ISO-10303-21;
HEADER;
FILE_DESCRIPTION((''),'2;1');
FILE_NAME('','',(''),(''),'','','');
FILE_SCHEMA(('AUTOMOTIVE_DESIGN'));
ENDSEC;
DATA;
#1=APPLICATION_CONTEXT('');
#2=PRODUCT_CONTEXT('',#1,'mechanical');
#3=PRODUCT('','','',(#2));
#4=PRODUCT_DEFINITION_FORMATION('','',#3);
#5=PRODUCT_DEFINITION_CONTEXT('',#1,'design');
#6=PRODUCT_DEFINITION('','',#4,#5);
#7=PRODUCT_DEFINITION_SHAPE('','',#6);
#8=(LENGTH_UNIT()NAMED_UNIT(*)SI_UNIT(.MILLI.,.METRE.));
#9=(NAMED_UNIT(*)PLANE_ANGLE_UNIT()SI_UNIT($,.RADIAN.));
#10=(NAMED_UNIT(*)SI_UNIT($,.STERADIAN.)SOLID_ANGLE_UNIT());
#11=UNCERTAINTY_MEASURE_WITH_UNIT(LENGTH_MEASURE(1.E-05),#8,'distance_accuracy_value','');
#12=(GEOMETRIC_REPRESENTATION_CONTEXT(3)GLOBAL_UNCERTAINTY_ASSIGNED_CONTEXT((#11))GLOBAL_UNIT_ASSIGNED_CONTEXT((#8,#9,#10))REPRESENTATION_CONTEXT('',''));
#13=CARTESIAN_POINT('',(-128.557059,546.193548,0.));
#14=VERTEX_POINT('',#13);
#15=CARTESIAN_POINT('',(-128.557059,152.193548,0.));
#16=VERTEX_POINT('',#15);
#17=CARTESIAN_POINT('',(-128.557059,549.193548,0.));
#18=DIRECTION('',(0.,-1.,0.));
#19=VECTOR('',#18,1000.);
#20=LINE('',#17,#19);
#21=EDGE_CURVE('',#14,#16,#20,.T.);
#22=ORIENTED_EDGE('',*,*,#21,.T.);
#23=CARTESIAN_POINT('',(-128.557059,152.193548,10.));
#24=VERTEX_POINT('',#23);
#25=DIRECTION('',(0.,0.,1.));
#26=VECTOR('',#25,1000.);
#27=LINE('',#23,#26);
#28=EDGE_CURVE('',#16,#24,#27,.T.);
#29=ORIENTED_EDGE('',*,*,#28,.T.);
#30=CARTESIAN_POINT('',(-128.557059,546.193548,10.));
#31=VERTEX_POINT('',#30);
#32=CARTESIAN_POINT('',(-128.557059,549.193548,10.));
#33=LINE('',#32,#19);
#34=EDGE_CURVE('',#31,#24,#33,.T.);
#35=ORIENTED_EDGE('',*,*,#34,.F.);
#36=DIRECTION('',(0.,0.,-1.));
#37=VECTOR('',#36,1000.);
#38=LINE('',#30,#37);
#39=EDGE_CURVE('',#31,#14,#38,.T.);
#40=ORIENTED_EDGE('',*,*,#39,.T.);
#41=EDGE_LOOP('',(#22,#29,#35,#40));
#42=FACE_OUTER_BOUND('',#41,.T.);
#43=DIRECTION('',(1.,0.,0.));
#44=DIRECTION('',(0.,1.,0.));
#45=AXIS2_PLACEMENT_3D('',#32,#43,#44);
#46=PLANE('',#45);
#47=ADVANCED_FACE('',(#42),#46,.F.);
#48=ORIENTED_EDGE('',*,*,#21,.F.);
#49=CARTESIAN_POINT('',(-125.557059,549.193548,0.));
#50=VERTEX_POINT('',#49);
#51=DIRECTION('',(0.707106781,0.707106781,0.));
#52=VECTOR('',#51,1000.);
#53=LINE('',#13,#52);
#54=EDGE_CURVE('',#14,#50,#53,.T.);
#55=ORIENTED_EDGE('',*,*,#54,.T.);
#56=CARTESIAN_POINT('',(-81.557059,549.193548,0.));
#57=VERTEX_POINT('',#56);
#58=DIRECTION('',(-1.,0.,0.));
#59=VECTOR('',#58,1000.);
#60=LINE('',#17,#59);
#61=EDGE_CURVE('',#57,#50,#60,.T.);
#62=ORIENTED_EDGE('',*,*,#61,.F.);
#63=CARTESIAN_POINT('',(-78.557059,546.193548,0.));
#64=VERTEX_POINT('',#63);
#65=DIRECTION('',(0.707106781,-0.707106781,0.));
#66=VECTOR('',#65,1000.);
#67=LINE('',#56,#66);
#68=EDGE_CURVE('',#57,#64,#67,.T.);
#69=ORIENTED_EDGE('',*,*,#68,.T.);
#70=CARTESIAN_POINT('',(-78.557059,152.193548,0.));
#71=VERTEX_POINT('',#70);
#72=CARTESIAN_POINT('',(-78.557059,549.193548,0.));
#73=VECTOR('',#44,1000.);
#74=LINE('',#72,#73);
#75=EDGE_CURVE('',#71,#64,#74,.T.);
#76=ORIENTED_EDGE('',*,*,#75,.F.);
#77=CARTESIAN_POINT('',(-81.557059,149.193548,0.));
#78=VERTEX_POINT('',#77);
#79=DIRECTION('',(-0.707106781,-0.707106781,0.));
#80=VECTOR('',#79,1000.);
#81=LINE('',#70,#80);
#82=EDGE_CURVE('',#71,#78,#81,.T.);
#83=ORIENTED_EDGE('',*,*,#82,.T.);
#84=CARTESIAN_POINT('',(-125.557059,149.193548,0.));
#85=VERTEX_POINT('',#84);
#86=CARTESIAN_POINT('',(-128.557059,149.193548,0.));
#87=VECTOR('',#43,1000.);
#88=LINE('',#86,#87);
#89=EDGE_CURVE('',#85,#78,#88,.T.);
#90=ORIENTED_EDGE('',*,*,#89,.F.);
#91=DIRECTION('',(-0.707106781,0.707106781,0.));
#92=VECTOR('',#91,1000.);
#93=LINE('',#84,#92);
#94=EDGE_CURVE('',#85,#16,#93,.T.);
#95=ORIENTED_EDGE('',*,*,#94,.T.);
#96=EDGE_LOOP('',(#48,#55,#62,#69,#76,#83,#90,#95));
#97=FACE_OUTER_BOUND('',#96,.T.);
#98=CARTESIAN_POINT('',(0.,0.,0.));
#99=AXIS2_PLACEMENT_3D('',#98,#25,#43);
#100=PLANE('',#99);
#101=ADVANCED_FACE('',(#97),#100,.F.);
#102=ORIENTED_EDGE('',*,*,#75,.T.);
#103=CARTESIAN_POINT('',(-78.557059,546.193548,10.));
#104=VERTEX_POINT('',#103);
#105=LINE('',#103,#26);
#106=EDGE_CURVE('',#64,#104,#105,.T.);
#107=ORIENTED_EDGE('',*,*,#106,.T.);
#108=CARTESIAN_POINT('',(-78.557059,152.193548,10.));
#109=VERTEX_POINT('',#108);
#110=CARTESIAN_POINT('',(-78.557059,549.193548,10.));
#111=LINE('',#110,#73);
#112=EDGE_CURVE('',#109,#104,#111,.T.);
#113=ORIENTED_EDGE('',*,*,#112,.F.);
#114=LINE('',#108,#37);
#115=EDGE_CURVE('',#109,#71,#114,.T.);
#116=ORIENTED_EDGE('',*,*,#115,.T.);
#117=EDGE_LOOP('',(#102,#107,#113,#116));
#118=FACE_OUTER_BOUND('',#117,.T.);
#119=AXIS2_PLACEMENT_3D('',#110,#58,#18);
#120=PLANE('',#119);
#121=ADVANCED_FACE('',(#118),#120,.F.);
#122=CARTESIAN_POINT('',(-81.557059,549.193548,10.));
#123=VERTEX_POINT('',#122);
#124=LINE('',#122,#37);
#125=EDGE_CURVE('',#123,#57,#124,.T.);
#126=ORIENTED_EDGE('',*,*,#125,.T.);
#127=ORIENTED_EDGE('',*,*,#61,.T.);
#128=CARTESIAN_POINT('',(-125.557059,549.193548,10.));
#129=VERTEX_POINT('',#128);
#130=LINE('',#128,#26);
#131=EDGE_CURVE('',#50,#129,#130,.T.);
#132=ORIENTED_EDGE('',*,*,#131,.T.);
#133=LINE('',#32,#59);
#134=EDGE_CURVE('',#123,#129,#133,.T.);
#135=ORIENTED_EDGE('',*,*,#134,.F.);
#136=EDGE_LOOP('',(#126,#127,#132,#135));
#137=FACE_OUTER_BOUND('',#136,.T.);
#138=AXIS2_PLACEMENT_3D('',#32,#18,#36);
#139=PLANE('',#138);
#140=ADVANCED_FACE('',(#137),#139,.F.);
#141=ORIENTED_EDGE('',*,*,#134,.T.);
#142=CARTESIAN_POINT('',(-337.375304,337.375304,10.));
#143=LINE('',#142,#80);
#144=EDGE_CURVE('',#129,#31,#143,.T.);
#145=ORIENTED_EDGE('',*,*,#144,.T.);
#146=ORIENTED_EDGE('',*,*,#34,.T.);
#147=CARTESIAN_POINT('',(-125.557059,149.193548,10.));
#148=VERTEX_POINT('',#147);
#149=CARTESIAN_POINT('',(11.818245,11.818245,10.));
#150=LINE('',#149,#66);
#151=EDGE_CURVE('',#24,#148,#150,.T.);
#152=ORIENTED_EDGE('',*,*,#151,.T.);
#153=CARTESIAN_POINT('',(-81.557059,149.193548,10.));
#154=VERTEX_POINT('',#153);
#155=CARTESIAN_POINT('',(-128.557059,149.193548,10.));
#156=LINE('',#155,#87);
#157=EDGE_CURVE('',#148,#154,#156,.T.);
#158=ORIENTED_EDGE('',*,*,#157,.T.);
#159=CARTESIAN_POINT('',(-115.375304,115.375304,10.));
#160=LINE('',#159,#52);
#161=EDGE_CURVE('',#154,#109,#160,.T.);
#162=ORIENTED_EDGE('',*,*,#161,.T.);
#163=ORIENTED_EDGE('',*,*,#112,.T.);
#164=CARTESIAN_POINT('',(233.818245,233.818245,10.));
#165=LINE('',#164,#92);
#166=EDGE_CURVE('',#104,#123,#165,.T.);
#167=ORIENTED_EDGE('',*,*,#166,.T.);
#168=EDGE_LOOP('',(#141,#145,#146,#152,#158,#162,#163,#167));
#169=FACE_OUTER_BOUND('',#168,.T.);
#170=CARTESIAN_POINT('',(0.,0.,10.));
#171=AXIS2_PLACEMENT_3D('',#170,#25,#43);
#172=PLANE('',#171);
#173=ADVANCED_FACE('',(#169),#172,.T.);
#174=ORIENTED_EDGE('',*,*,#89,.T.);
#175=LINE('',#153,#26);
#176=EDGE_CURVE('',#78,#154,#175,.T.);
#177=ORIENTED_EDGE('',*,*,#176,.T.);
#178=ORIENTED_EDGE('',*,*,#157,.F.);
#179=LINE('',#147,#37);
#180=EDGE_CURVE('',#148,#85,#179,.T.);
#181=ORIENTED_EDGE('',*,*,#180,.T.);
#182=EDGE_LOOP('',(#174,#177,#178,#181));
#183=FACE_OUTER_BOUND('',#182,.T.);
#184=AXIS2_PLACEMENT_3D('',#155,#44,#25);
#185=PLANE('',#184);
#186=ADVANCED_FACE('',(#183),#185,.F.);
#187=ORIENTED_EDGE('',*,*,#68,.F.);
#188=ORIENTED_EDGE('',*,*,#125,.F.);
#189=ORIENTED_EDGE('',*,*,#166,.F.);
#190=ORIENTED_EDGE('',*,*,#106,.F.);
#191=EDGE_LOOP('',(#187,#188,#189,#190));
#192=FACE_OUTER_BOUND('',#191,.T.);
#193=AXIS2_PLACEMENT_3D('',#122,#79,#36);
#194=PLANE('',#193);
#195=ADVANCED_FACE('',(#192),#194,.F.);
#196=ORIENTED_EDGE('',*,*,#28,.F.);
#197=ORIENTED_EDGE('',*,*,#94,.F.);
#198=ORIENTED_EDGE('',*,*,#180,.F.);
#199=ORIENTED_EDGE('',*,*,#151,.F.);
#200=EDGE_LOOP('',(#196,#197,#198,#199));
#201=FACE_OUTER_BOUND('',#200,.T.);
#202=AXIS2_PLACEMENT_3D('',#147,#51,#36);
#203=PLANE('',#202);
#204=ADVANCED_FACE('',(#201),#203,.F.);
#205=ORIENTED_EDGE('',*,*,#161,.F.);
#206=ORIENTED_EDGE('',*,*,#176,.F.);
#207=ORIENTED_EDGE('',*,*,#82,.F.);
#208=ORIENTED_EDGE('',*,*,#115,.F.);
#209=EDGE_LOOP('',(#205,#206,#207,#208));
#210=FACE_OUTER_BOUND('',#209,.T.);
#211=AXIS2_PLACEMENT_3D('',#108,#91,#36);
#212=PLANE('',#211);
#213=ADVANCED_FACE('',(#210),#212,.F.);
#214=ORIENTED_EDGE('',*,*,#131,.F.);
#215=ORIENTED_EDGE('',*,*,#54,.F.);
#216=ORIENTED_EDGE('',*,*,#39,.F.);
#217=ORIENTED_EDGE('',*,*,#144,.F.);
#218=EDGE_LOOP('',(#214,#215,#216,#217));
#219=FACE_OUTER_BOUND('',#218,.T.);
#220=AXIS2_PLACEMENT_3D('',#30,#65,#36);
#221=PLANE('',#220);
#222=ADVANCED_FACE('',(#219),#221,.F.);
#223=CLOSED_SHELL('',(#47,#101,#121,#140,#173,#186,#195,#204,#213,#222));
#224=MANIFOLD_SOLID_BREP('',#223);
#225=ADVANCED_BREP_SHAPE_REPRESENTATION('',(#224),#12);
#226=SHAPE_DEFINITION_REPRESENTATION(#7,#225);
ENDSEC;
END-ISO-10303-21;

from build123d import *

# Parameters (mm, degrees)
SKETCH1_W           = 50
SKETCH1_H           = 400
BOSS_EXTRUDE1_DEPTH = 10
CHAMFER1_SIZE       = 3


with BuildPart() as part:
    # Sketch1 → Boss-Extrude1 (new body)
    with BuildSketch(Plane.XY):
        with Locations((-103.557058929, 349.193548387)):
            Rectangle(SKETCH1_W, SKETCH1_H)
    extrude(amount=BOSS_EXTRUDE1_DEPTH)

    # Chamfer1
    chamfer1_edges = [part.edges().sort_by_distance(p)[0] for p in [
        (-128.557058929, 549.193548387, 5),
        (-78.557058929, 549.193548387, 5),
        (-78.557058929, 149.193548387, 5),
        (-128.557058929, 149.193548387, 5),
    ]]
    chamfer(chamfer1_edges, length=CHAMFER1_SIZE)


solid = part.part
